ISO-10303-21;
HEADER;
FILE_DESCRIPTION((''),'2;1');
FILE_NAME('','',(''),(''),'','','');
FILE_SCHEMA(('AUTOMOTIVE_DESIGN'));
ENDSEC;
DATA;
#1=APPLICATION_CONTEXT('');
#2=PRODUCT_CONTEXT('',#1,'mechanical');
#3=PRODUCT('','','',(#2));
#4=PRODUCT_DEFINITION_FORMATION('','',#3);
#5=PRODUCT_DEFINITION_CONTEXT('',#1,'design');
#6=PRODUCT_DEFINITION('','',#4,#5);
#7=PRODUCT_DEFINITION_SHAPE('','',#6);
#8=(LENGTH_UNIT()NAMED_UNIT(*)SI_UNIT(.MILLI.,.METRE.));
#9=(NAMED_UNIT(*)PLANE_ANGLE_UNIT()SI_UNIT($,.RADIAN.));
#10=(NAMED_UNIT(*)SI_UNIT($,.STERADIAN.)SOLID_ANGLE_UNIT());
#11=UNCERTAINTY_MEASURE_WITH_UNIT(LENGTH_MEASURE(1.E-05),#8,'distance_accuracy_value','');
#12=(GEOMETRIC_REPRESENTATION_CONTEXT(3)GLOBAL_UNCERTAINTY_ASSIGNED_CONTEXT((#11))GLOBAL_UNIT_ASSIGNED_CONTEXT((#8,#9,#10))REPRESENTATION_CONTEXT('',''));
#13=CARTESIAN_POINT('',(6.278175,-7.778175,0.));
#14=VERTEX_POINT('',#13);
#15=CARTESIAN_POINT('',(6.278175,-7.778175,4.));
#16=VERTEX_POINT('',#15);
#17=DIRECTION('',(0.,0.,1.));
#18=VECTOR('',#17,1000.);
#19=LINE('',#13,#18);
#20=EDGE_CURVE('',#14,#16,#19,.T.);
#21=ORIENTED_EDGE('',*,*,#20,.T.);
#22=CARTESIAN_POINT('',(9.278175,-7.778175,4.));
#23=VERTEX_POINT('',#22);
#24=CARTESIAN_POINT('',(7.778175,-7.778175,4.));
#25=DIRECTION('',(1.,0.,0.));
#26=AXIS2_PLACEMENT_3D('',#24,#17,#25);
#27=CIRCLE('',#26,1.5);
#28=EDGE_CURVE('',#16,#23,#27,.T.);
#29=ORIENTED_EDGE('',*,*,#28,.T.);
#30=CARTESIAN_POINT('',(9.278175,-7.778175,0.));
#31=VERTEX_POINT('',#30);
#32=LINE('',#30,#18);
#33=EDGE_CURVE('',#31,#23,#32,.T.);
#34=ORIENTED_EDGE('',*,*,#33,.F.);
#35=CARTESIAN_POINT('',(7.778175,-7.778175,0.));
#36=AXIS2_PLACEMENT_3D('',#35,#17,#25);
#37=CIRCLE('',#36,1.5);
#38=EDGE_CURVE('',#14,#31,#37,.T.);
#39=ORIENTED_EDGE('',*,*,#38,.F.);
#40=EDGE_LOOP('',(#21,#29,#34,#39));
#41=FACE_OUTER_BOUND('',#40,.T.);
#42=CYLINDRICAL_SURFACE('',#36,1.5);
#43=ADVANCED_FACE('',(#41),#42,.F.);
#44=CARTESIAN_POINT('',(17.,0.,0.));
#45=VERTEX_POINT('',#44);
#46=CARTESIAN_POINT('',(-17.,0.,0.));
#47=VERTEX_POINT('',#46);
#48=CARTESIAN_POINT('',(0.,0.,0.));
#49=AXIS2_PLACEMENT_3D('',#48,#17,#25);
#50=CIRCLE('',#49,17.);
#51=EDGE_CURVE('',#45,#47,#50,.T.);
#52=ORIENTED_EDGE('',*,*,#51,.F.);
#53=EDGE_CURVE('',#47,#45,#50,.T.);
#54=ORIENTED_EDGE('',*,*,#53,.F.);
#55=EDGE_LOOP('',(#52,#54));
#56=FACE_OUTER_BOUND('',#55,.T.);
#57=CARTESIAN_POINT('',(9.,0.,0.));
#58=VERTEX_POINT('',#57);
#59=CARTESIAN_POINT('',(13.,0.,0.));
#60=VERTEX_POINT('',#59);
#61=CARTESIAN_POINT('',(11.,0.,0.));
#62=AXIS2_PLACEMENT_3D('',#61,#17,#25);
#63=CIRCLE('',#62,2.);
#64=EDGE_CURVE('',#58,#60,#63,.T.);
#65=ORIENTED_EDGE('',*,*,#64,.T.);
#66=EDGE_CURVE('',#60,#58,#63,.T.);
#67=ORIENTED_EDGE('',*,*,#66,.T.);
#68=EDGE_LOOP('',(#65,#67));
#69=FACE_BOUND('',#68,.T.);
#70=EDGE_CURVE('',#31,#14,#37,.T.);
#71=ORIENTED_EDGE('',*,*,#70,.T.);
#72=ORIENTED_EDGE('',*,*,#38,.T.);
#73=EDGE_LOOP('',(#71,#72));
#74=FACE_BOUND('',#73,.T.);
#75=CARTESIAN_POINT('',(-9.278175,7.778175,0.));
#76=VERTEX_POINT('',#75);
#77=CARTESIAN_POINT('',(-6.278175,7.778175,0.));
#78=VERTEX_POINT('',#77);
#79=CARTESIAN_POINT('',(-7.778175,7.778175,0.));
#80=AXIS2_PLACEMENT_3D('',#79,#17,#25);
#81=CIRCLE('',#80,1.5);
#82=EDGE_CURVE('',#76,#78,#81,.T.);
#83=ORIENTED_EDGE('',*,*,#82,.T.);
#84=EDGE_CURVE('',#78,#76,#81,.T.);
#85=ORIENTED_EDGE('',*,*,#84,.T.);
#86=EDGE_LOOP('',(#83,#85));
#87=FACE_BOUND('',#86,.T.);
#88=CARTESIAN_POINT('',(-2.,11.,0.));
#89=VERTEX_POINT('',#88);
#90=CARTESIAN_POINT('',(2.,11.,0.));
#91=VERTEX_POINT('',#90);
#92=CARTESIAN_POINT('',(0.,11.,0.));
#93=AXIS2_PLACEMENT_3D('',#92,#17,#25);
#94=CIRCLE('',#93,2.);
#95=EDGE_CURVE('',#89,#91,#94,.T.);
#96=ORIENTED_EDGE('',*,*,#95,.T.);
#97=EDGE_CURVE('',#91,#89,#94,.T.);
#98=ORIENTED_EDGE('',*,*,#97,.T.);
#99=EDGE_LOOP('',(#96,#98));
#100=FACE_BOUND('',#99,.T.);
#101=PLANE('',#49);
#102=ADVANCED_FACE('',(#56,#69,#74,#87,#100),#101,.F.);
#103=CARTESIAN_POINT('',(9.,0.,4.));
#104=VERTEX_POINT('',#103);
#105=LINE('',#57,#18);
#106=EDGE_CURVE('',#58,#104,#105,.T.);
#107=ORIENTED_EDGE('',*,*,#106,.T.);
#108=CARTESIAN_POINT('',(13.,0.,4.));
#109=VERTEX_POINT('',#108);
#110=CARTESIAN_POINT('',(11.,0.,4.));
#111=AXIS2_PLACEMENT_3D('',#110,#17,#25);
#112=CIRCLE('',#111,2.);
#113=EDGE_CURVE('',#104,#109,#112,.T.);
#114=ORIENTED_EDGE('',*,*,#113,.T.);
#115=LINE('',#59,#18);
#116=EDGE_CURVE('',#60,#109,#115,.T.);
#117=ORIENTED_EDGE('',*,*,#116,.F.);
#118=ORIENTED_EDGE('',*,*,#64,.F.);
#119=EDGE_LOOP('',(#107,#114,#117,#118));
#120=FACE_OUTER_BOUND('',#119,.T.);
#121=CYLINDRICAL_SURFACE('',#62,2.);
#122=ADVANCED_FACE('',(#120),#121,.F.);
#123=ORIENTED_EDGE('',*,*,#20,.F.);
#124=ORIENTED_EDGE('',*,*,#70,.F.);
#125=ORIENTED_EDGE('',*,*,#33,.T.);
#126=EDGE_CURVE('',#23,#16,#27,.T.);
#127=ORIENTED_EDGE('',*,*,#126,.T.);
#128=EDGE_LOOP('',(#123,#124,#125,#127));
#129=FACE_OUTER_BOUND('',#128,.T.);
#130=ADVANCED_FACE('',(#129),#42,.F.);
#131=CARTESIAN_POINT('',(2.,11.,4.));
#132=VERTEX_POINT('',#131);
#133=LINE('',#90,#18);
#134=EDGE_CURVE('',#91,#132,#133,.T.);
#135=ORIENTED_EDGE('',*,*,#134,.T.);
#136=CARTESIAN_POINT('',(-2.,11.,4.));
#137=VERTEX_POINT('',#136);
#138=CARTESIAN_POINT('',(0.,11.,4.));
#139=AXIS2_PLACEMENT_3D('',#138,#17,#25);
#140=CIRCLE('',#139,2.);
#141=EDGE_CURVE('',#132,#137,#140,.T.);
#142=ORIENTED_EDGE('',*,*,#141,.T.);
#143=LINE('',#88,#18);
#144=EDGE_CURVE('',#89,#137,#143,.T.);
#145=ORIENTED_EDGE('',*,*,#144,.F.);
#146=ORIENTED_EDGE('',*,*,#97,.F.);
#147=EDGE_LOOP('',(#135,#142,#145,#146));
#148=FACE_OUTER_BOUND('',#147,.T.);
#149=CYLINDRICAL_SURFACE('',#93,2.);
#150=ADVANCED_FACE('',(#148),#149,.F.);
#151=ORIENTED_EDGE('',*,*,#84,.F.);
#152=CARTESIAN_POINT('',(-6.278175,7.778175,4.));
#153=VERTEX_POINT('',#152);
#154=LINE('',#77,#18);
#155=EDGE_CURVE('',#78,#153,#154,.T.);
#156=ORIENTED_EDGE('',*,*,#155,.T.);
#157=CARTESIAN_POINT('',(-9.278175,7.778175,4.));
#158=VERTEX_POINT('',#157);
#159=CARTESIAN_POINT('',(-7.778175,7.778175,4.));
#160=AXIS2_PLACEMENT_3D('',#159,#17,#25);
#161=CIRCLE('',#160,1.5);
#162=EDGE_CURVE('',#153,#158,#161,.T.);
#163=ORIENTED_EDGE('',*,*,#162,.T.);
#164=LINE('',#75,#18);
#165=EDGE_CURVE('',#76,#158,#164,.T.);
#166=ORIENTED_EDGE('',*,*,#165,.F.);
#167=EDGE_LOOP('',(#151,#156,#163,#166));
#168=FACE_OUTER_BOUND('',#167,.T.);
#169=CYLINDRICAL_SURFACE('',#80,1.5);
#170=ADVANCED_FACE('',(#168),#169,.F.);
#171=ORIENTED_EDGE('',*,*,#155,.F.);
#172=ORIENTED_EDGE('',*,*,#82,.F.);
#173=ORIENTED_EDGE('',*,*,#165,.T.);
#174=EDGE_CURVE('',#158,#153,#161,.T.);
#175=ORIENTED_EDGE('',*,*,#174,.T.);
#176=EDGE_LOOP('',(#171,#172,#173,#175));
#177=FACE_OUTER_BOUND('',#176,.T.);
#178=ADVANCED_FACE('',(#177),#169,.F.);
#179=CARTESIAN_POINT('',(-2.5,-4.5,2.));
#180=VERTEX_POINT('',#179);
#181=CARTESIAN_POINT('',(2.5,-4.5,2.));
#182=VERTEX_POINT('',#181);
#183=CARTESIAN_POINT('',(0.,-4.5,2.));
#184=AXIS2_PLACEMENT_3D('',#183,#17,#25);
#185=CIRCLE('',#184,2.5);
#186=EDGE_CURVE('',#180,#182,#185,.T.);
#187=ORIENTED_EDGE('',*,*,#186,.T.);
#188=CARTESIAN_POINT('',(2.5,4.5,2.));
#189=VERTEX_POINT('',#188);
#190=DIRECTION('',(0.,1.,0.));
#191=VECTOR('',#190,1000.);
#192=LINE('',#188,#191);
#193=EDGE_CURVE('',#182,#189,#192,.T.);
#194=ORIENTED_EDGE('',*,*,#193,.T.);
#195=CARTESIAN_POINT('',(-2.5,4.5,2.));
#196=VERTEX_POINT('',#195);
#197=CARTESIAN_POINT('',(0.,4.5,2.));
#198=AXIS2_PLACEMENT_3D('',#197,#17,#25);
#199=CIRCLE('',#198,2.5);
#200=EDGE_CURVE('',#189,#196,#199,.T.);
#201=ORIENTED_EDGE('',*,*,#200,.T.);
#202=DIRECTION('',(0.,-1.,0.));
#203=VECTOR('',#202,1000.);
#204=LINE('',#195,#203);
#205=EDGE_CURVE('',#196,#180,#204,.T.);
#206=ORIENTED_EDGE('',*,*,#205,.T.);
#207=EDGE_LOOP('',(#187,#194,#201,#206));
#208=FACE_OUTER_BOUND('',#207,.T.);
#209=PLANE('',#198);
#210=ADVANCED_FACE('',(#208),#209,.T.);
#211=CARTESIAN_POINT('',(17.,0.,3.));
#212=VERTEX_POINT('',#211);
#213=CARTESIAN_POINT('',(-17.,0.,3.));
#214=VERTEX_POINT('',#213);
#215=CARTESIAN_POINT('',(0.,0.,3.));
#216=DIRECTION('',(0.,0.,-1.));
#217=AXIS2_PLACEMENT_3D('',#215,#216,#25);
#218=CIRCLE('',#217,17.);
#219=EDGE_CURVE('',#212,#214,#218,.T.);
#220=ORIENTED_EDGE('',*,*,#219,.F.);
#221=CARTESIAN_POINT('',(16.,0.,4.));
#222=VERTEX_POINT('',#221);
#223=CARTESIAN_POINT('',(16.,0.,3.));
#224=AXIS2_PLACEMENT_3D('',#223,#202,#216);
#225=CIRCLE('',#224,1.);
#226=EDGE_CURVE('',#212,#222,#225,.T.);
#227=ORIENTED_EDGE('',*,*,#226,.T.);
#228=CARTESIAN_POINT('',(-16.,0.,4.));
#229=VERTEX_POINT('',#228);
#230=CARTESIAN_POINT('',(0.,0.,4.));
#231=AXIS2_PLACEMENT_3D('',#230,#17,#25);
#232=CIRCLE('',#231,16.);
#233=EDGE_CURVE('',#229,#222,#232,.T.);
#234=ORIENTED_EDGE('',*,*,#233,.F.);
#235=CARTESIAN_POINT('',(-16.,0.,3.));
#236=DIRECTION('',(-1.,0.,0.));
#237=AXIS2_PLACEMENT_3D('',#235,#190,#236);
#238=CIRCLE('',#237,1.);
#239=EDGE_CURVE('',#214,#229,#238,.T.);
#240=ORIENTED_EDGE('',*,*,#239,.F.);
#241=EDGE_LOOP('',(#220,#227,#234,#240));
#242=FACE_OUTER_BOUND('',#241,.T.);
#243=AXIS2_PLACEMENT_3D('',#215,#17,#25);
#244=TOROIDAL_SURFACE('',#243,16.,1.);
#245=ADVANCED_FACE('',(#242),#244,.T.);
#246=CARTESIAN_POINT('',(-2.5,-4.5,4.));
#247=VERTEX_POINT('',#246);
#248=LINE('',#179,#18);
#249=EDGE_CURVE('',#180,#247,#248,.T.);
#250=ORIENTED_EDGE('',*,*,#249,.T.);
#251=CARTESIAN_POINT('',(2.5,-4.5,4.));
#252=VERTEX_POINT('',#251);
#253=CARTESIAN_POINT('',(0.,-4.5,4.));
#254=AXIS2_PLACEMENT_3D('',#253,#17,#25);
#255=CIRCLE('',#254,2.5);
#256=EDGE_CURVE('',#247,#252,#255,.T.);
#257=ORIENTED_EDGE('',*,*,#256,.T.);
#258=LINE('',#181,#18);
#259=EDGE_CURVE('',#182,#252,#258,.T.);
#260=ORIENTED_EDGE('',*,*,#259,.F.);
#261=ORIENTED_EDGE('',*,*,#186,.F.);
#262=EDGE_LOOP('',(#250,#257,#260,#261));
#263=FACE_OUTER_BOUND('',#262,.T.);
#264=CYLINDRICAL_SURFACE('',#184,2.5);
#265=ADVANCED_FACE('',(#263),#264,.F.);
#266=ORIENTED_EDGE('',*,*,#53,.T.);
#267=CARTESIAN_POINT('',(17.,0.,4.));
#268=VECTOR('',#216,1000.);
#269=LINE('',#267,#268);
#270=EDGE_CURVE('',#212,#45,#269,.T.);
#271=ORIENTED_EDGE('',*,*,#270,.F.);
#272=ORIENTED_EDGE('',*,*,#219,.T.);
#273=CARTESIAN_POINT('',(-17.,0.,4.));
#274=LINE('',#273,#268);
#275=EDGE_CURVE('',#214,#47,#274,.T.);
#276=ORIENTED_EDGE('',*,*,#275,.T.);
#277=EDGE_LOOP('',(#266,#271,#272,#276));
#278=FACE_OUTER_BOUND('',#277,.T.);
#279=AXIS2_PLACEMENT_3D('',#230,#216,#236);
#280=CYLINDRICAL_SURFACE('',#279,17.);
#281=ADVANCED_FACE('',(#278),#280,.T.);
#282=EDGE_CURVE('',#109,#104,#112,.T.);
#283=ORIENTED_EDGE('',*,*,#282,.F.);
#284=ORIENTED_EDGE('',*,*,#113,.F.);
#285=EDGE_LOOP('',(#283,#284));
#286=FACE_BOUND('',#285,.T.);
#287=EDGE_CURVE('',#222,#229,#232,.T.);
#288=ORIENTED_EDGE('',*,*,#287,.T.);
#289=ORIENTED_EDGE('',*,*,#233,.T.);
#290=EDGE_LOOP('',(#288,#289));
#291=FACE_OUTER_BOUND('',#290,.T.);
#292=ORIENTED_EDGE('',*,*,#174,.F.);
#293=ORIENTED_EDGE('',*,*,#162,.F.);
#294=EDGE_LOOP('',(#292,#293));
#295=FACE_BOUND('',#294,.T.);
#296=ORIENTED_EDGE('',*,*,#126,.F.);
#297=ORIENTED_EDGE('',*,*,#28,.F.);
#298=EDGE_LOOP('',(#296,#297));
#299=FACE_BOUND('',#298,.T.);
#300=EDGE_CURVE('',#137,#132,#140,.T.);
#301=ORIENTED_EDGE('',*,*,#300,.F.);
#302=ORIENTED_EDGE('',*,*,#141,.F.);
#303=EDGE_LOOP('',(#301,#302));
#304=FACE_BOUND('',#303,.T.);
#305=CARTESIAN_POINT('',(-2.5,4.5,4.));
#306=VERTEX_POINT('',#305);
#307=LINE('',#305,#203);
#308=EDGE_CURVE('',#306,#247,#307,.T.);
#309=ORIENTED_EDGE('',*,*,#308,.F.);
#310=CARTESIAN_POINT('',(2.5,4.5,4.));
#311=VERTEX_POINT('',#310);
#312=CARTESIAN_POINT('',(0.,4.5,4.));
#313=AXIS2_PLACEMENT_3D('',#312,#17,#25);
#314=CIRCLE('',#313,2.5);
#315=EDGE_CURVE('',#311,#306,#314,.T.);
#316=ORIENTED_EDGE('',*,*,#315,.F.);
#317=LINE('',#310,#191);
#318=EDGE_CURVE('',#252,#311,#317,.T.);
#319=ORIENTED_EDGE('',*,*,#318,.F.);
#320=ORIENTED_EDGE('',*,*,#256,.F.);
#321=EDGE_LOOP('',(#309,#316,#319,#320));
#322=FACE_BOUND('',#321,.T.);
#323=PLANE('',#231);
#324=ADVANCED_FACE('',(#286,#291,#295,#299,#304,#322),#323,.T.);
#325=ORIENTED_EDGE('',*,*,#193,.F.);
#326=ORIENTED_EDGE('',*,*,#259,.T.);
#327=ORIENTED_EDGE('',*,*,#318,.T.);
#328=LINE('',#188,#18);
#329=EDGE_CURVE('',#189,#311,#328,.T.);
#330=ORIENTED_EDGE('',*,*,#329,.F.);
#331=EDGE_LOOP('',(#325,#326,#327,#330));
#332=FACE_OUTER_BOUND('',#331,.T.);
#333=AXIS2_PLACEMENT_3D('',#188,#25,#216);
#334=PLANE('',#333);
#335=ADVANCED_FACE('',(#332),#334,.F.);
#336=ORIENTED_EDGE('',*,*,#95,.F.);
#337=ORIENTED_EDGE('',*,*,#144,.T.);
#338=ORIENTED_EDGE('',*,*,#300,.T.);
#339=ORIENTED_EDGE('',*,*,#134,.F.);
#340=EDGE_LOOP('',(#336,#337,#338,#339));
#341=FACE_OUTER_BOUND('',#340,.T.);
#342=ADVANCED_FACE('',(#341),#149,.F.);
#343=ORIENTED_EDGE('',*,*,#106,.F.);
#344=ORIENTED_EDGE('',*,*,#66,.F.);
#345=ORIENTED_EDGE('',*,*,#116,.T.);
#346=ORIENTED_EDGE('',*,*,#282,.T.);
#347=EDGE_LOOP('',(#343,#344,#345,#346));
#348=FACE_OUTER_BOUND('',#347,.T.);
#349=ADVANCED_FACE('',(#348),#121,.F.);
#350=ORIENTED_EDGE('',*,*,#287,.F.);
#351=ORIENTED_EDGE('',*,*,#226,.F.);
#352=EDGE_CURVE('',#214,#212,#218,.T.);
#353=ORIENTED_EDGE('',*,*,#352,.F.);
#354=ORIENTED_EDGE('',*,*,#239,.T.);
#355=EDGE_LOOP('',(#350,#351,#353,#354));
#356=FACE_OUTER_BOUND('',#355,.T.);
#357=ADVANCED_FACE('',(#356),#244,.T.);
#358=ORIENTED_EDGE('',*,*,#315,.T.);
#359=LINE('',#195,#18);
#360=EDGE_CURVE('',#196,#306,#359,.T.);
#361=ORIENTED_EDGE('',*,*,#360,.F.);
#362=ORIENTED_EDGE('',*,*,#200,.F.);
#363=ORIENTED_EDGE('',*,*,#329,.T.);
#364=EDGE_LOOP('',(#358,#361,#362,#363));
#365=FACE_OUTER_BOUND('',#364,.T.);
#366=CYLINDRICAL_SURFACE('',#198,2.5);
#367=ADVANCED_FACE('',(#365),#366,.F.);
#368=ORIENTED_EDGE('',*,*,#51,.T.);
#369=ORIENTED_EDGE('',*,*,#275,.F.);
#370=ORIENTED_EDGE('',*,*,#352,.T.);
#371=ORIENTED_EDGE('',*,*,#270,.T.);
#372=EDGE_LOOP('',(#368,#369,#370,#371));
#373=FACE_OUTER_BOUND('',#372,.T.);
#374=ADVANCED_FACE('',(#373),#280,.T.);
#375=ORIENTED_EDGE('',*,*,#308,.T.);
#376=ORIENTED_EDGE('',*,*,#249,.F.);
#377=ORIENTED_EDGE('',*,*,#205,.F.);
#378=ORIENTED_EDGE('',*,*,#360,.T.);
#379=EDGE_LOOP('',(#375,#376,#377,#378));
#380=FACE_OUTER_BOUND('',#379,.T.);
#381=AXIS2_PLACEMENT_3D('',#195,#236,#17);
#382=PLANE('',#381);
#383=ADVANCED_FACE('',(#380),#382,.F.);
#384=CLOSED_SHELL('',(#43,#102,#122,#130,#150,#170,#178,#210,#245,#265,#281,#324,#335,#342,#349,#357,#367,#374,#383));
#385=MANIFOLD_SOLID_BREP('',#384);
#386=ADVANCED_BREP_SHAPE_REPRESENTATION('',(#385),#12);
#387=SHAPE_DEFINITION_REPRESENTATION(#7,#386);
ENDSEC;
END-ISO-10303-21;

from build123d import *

# Parameters (mm, degrees)
SKETCH1_R           = 17
BOSS_EXTRUDE1_DEPTH = 4
CUT_EXTRUDE1_DEPTH  = 2
SKETCH3_R           = 2
SKETCH3_R_2         = 1.5
CUT_EXTRUDE2_DEPTH  = 4
FILLET1_R           = 1


with BuildPart() as part:
    # Sketch1 → Boss-Extrude1 (new body)
    with BuildSketch(Plane.XY):
        Circle(SKETCH1_R)
    extrude(amount=BOSS_EXTRUDE1_DEPTH)

    # Sketch2 → Cut-Extrude1 (cut)
    with BuildSketch(Plane.XY.offset(4)):
        with BuildLine():
            Line((2.5, 4.5), (2.5, -4.5))
            ThreePointArc((2.5, -4.5), (0, -7), (-2.5, -4.5))
            Line((-2.5, -4.5), (-2.5, 4.5))
            ThreePointArc((-2.5, 4.5), (0, 7), (2.5, 4.5))
        make_face()
    extrude(amount=-CUT_EXTRUDE1_DEPTH, mode=Mode.SUBTRACT)

    # Sketch3 → Cut-Extrude2 (cut)
    with BuildSketch(Plane.XY.offset(4)):
        with Locations((0, 11)):
            Circle(SKETCH3_R)
        with Locations((11, 0)):
            Circle(SKETCH3_R)
        with Locations((-7.778174593, 7.778174593)):
            Circle(SKETCH3_R_2)
        with Locations((7.778174593, -7.778174593)):
            Circle(SKETCH3_R_2)
    extrude(amount=-CUT_EXTRUDE2_DEPTH, mode=Mode.SUBTRACT)

    # Fillet1
    fillet1_edges = [part.edges().sort_by_distance(p)[0] for p in [
        (-17, 0, 4),
    ]]
    fillet(fillet1_edges, radius=FILLET1_R)


solid = part.part
